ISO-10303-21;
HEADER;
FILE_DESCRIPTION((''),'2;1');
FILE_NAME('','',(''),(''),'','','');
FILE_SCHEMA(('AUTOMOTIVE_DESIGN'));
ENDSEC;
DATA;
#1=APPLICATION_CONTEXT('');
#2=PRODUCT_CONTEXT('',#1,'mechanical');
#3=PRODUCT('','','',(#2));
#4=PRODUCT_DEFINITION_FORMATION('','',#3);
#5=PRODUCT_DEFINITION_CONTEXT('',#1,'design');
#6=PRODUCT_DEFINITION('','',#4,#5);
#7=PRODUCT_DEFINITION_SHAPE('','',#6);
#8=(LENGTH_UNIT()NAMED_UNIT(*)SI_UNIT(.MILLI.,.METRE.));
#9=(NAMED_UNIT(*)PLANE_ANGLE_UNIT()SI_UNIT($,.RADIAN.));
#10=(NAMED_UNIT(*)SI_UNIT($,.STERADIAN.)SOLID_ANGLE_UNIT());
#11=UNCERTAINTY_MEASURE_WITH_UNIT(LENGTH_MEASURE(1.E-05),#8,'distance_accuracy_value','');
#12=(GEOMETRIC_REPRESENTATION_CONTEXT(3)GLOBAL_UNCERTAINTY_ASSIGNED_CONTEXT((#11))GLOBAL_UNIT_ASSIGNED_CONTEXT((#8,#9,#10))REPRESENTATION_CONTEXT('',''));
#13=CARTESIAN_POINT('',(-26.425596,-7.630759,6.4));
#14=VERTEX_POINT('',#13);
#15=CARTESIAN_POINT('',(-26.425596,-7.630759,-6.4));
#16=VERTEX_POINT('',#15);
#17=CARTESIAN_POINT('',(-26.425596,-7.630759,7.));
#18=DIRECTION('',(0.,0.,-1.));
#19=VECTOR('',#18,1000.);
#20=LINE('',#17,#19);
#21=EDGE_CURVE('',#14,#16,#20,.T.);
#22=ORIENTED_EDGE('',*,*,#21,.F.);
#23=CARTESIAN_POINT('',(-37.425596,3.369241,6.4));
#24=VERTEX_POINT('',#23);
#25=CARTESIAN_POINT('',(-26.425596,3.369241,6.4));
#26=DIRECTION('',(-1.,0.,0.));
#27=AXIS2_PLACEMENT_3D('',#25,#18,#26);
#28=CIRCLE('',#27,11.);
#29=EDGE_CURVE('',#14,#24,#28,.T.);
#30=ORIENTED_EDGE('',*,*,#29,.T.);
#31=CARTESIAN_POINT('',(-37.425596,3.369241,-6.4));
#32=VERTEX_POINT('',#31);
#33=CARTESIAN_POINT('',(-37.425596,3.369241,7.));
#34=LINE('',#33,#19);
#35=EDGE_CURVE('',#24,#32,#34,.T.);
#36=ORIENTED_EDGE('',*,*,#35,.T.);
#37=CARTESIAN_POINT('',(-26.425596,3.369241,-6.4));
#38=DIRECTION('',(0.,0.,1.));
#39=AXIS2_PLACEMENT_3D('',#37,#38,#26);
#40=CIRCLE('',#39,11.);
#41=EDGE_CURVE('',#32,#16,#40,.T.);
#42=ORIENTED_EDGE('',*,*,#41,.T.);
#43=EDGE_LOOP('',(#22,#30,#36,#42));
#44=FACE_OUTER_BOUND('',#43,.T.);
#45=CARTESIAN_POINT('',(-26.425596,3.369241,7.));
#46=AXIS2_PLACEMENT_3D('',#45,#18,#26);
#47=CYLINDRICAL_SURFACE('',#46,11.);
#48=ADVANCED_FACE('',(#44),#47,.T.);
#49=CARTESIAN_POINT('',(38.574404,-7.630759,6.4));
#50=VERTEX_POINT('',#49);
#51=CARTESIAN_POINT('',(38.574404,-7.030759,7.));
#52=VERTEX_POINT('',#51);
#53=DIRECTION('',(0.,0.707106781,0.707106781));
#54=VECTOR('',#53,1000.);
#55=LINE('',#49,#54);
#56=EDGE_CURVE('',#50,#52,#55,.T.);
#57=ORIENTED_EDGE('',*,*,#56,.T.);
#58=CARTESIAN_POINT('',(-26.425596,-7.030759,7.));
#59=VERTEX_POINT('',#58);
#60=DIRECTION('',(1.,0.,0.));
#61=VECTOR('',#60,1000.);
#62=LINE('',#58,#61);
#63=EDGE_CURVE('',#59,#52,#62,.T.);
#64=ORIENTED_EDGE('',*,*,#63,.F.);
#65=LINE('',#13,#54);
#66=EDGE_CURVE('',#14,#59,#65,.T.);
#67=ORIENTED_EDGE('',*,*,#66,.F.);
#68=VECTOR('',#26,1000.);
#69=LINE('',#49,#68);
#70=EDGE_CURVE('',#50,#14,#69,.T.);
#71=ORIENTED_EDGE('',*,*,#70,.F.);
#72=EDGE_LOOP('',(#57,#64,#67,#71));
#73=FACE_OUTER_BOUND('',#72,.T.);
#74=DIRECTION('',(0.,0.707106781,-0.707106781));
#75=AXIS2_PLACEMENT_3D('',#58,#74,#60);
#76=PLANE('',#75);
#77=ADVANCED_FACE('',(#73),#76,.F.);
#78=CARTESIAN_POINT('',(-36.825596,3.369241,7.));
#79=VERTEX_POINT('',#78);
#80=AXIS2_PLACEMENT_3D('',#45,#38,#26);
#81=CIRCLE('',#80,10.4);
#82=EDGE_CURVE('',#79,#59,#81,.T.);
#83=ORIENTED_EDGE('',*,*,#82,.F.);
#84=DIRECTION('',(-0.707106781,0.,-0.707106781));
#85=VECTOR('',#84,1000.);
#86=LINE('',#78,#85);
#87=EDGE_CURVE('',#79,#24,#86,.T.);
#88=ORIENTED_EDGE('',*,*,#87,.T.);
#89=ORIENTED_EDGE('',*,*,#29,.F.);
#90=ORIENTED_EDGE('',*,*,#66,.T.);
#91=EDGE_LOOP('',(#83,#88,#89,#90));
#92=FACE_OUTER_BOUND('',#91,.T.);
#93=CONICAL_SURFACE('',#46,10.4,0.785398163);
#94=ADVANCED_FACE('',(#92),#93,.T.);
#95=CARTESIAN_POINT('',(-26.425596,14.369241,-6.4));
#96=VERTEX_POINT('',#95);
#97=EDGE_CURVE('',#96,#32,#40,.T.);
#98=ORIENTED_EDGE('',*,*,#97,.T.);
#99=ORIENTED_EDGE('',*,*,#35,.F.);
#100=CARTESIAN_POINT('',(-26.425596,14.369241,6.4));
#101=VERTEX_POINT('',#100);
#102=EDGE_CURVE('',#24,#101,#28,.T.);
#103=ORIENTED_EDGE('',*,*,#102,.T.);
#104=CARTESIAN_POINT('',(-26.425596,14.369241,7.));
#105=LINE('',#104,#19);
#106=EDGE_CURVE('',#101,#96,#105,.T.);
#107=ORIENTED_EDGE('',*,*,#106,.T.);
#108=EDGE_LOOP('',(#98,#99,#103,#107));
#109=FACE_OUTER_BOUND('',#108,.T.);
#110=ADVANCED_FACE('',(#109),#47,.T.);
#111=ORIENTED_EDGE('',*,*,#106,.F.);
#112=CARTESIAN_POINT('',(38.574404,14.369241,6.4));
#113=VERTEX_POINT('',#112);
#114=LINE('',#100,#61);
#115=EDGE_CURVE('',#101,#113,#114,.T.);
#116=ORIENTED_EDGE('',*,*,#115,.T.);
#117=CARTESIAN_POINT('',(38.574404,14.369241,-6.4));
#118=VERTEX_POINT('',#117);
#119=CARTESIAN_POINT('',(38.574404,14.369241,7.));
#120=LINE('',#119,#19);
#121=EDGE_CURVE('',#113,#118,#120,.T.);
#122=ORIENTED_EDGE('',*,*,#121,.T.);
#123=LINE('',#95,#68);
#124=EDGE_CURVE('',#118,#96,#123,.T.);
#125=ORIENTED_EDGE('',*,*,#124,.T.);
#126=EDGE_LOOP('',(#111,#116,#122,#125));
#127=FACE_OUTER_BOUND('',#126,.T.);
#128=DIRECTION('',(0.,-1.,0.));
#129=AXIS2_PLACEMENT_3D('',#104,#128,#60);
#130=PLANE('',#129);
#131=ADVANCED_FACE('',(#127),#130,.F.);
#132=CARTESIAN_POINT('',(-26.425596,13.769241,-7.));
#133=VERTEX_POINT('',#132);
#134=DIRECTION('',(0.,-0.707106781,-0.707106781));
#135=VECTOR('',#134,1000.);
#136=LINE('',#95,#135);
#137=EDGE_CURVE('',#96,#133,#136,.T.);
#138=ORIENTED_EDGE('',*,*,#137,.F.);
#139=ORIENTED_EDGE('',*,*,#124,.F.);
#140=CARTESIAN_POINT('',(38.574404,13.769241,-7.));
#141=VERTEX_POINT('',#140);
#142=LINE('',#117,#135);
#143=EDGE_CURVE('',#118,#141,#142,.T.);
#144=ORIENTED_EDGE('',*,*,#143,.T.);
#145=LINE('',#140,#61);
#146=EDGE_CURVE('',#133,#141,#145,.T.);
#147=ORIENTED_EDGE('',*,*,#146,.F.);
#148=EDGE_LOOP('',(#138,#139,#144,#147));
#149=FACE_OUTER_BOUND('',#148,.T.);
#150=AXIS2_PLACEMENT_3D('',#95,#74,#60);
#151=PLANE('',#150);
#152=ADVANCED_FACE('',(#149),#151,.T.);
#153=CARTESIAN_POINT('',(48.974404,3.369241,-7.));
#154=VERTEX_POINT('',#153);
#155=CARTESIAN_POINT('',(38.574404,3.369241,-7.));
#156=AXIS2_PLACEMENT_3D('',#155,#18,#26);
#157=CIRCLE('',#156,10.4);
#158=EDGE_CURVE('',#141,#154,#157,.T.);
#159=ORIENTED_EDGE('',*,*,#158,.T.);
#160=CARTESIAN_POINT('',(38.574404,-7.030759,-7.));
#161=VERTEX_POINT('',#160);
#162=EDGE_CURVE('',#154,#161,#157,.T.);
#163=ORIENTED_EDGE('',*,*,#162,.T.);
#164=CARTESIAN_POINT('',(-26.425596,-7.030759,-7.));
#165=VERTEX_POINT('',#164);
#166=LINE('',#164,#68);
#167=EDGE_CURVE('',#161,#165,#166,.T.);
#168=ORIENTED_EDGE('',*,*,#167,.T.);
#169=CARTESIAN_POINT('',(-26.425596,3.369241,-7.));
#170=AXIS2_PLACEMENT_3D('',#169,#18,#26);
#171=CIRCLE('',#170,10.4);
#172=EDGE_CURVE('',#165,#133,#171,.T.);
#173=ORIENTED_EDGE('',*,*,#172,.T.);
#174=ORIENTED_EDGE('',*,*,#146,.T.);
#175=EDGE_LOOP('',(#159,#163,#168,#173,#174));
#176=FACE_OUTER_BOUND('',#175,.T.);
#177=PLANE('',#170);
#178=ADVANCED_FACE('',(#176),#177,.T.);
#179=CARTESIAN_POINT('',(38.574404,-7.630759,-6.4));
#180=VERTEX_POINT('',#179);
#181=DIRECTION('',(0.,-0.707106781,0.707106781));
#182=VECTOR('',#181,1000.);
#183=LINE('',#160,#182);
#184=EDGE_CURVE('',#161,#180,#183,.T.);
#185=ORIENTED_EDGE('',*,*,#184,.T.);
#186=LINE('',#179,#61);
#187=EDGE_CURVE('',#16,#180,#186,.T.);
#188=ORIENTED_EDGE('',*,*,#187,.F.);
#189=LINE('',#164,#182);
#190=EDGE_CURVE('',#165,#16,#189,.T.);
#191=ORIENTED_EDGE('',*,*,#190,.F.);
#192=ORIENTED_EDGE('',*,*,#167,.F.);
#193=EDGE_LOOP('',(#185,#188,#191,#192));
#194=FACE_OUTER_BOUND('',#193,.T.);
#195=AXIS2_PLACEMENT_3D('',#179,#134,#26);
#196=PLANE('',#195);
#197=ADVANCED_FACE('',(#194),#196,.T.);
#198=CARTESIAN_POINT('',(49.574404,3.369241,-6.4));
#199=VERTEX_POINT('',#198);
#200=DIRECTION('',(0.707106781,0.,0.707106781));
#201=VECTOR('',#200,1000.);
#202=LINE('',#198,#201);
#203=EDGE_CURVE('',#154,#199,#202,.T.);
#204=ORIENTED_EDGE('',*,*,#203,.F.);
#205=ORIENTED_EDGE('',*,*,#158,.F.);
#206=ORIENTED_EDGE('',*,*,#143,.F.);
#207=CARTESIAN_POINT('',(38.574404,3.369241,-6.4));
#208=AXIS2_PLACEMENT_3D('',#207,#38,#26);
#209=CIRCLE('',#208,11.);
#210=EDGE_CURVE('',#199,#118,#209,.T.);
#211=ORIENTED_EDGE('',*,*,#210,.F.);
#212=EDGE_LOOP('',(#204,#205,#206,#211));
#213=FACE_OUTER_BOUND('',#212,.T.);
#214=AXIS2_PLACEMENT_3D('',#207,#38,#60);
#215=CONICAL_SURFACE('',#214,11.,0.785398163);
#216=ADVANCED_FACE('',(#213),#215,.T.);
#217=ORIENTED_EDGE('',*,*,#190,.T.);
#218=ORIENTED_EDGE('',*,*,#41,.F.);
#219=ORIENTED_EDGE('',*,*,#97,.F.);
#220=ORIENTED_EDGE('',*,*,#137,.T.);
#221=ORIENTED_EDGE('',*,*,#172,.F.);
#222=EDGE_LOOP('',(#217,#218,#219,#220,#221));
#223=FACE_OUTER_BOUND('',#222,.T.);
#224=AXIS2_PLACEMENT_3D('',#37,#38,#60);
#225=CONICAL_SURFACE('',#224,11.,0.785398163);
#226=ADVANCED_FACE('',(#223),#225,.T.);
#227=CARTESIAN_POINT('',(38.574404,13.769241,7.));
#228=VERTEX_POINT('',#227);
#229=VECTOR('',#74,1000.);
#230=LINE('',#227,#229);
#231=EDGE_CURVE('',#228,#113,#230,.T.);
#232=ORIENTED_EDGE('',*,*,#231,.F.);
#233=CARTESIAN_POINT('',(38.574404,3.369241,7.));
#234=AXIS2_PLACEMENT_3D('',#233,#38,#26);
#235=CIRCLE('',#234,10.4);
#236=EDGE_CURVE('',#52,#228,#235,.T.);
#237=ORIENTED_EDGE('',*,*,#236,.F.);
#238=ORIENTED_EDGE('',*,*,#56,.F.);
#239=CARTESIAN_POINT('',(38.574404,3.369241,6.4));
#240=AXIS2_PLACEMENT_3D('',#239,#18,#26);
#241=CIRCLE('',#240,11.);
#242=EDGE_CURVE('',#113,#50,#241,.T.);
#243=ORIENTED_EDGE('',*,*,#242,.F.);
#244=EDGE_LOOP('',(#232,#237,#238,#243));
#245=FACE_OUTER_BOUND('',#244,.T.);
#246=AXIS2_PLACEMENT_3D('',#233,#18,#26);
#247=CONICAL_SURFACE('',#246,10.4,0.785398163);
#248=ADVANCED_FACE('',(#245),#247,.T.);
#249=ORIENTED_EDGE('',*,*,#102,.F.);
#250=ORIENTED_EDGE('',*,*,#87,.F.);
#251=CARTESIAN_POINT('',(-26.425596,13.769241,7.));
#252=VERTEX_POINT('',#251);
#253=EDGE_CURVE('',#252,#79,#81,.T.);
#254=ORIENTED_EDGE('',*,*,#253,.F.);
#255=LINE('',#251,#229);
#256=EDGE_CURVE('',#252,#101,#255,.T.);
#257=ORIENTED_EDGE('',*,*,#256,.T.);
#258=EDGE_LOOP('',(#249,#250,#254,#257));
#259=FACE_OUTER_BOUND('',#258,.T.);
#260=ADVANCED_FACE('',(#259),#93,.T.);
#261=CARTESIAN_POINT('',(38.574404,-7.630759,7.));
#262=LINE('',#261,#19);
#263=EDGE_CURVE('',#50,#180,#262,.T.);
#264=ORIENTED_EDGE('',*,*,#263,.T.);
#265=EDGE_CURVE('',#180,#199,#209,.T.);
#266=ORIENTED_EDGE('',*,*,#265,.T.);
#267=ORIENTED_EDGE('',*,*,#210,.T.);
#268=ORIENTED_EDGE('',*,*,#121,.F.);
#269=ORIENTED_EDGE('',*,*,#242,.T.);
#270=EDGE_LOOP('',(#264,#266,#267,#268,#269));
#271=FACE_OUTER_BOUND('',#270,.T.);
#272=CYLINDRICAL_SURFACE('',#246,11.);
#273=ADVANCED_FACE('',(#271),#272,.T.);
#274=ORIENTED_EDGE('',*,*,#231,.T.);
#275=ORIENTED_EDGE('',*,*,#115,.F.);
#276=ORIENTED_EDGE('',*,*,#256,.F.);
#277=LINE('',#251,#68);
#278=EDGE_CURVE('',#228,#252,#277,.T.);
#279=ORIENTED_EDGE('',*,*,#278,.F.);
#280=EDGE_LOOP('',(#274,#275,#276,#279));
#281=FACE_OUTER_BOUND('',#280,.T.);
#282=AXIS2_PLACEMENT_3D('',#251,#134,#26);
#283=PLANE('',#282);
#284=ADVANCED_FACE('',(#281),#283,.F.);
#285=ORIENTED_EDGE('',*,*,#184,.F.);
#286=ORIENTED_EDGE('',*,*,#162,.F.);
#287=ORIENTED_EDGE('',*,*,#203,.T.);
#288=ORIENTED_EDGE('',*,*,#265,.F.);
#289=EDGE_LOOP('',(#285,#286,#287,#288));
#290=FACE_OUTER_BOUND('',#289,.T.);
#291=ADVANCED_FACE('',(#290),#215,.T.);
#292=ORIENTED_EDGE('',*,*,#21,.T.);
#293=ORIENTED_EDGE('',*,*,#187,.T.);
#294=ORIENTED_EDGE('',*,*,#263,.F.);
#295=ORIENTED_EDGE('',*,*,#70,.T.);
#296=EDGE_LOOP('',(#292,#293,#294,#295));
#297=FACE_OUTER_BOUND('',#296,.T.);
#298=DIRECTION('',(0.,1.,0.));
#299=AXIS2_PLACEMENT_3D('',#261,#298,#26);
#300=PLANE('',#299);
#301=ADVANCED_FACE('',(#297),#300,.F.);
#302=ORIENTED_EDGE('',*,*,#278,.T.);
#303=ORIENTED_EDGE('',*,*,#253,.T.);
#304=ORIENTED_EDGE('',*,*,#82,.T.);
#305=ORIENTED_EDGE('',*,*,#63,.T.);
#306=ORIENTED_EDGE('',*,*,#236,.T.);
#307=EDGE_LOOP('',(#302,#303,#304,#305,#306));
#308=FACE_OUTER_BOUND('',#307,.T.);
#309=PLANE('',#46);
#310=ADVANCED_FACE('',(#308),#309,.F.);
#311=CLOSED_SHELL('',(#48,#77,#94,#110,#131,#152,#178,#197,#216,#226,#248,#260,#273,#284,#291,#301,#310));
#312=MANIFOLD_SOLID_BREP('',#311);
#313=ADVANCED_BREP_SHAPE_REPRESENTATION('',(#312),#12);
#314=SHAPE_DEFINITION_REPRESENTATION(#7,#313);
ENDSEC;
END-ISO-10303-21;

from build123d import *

# Parameters (mm, degrees)
BOSS_EXTRUDE1_DEPTH = 7
CHAMFER1_SIZE       = 0.6


with BuildPart() as part:
    # Sketch1 → Boss-Extrude1 (new, symmetric)
    with BuildSketch(Plane.XY):
        with BuildLine():
            Line((-26.425596314, 14.36924081), (38.574403686, 14.36924081))
            ThreePointArc((38.574403686, 14.36924081), (49.574403686, 3.36924081), (38.574403686, -7.63075919))
            Line((38.574403686, -7.63075919), (-26.425596314, -7.63075919))
            ThreePointArc((-26.425596314, -7.63075919), (-37.425596314, 3.36924081), (-26.425596314, 14.36924081))
        make_face()
    extrude(amount=BOSS_EXTRUDE1_DEPTH, both=True)

    # Chamfer1
    chamfer1_edges = [part.edges().sort_by_distance(p)[0] for p in [
        (49.574403686, 3.36924081, 7),
        (6.074403686, 14.36924081, 7),
        (-37.425596314, 3.36924081, 7),
        (6.074403686, 14.36924081, -7),
        (49.574403686, 3.36924081, -7),
        (6.074403686, -7.63075919, -7),
        (-37.425596314, 3.36924081, -7),
        (6.074403686, -7.63075919, 7),
    ]]
    chamfer(chamfer1_edges, length=CHAMFER1_SIZE)


solid = part.part
